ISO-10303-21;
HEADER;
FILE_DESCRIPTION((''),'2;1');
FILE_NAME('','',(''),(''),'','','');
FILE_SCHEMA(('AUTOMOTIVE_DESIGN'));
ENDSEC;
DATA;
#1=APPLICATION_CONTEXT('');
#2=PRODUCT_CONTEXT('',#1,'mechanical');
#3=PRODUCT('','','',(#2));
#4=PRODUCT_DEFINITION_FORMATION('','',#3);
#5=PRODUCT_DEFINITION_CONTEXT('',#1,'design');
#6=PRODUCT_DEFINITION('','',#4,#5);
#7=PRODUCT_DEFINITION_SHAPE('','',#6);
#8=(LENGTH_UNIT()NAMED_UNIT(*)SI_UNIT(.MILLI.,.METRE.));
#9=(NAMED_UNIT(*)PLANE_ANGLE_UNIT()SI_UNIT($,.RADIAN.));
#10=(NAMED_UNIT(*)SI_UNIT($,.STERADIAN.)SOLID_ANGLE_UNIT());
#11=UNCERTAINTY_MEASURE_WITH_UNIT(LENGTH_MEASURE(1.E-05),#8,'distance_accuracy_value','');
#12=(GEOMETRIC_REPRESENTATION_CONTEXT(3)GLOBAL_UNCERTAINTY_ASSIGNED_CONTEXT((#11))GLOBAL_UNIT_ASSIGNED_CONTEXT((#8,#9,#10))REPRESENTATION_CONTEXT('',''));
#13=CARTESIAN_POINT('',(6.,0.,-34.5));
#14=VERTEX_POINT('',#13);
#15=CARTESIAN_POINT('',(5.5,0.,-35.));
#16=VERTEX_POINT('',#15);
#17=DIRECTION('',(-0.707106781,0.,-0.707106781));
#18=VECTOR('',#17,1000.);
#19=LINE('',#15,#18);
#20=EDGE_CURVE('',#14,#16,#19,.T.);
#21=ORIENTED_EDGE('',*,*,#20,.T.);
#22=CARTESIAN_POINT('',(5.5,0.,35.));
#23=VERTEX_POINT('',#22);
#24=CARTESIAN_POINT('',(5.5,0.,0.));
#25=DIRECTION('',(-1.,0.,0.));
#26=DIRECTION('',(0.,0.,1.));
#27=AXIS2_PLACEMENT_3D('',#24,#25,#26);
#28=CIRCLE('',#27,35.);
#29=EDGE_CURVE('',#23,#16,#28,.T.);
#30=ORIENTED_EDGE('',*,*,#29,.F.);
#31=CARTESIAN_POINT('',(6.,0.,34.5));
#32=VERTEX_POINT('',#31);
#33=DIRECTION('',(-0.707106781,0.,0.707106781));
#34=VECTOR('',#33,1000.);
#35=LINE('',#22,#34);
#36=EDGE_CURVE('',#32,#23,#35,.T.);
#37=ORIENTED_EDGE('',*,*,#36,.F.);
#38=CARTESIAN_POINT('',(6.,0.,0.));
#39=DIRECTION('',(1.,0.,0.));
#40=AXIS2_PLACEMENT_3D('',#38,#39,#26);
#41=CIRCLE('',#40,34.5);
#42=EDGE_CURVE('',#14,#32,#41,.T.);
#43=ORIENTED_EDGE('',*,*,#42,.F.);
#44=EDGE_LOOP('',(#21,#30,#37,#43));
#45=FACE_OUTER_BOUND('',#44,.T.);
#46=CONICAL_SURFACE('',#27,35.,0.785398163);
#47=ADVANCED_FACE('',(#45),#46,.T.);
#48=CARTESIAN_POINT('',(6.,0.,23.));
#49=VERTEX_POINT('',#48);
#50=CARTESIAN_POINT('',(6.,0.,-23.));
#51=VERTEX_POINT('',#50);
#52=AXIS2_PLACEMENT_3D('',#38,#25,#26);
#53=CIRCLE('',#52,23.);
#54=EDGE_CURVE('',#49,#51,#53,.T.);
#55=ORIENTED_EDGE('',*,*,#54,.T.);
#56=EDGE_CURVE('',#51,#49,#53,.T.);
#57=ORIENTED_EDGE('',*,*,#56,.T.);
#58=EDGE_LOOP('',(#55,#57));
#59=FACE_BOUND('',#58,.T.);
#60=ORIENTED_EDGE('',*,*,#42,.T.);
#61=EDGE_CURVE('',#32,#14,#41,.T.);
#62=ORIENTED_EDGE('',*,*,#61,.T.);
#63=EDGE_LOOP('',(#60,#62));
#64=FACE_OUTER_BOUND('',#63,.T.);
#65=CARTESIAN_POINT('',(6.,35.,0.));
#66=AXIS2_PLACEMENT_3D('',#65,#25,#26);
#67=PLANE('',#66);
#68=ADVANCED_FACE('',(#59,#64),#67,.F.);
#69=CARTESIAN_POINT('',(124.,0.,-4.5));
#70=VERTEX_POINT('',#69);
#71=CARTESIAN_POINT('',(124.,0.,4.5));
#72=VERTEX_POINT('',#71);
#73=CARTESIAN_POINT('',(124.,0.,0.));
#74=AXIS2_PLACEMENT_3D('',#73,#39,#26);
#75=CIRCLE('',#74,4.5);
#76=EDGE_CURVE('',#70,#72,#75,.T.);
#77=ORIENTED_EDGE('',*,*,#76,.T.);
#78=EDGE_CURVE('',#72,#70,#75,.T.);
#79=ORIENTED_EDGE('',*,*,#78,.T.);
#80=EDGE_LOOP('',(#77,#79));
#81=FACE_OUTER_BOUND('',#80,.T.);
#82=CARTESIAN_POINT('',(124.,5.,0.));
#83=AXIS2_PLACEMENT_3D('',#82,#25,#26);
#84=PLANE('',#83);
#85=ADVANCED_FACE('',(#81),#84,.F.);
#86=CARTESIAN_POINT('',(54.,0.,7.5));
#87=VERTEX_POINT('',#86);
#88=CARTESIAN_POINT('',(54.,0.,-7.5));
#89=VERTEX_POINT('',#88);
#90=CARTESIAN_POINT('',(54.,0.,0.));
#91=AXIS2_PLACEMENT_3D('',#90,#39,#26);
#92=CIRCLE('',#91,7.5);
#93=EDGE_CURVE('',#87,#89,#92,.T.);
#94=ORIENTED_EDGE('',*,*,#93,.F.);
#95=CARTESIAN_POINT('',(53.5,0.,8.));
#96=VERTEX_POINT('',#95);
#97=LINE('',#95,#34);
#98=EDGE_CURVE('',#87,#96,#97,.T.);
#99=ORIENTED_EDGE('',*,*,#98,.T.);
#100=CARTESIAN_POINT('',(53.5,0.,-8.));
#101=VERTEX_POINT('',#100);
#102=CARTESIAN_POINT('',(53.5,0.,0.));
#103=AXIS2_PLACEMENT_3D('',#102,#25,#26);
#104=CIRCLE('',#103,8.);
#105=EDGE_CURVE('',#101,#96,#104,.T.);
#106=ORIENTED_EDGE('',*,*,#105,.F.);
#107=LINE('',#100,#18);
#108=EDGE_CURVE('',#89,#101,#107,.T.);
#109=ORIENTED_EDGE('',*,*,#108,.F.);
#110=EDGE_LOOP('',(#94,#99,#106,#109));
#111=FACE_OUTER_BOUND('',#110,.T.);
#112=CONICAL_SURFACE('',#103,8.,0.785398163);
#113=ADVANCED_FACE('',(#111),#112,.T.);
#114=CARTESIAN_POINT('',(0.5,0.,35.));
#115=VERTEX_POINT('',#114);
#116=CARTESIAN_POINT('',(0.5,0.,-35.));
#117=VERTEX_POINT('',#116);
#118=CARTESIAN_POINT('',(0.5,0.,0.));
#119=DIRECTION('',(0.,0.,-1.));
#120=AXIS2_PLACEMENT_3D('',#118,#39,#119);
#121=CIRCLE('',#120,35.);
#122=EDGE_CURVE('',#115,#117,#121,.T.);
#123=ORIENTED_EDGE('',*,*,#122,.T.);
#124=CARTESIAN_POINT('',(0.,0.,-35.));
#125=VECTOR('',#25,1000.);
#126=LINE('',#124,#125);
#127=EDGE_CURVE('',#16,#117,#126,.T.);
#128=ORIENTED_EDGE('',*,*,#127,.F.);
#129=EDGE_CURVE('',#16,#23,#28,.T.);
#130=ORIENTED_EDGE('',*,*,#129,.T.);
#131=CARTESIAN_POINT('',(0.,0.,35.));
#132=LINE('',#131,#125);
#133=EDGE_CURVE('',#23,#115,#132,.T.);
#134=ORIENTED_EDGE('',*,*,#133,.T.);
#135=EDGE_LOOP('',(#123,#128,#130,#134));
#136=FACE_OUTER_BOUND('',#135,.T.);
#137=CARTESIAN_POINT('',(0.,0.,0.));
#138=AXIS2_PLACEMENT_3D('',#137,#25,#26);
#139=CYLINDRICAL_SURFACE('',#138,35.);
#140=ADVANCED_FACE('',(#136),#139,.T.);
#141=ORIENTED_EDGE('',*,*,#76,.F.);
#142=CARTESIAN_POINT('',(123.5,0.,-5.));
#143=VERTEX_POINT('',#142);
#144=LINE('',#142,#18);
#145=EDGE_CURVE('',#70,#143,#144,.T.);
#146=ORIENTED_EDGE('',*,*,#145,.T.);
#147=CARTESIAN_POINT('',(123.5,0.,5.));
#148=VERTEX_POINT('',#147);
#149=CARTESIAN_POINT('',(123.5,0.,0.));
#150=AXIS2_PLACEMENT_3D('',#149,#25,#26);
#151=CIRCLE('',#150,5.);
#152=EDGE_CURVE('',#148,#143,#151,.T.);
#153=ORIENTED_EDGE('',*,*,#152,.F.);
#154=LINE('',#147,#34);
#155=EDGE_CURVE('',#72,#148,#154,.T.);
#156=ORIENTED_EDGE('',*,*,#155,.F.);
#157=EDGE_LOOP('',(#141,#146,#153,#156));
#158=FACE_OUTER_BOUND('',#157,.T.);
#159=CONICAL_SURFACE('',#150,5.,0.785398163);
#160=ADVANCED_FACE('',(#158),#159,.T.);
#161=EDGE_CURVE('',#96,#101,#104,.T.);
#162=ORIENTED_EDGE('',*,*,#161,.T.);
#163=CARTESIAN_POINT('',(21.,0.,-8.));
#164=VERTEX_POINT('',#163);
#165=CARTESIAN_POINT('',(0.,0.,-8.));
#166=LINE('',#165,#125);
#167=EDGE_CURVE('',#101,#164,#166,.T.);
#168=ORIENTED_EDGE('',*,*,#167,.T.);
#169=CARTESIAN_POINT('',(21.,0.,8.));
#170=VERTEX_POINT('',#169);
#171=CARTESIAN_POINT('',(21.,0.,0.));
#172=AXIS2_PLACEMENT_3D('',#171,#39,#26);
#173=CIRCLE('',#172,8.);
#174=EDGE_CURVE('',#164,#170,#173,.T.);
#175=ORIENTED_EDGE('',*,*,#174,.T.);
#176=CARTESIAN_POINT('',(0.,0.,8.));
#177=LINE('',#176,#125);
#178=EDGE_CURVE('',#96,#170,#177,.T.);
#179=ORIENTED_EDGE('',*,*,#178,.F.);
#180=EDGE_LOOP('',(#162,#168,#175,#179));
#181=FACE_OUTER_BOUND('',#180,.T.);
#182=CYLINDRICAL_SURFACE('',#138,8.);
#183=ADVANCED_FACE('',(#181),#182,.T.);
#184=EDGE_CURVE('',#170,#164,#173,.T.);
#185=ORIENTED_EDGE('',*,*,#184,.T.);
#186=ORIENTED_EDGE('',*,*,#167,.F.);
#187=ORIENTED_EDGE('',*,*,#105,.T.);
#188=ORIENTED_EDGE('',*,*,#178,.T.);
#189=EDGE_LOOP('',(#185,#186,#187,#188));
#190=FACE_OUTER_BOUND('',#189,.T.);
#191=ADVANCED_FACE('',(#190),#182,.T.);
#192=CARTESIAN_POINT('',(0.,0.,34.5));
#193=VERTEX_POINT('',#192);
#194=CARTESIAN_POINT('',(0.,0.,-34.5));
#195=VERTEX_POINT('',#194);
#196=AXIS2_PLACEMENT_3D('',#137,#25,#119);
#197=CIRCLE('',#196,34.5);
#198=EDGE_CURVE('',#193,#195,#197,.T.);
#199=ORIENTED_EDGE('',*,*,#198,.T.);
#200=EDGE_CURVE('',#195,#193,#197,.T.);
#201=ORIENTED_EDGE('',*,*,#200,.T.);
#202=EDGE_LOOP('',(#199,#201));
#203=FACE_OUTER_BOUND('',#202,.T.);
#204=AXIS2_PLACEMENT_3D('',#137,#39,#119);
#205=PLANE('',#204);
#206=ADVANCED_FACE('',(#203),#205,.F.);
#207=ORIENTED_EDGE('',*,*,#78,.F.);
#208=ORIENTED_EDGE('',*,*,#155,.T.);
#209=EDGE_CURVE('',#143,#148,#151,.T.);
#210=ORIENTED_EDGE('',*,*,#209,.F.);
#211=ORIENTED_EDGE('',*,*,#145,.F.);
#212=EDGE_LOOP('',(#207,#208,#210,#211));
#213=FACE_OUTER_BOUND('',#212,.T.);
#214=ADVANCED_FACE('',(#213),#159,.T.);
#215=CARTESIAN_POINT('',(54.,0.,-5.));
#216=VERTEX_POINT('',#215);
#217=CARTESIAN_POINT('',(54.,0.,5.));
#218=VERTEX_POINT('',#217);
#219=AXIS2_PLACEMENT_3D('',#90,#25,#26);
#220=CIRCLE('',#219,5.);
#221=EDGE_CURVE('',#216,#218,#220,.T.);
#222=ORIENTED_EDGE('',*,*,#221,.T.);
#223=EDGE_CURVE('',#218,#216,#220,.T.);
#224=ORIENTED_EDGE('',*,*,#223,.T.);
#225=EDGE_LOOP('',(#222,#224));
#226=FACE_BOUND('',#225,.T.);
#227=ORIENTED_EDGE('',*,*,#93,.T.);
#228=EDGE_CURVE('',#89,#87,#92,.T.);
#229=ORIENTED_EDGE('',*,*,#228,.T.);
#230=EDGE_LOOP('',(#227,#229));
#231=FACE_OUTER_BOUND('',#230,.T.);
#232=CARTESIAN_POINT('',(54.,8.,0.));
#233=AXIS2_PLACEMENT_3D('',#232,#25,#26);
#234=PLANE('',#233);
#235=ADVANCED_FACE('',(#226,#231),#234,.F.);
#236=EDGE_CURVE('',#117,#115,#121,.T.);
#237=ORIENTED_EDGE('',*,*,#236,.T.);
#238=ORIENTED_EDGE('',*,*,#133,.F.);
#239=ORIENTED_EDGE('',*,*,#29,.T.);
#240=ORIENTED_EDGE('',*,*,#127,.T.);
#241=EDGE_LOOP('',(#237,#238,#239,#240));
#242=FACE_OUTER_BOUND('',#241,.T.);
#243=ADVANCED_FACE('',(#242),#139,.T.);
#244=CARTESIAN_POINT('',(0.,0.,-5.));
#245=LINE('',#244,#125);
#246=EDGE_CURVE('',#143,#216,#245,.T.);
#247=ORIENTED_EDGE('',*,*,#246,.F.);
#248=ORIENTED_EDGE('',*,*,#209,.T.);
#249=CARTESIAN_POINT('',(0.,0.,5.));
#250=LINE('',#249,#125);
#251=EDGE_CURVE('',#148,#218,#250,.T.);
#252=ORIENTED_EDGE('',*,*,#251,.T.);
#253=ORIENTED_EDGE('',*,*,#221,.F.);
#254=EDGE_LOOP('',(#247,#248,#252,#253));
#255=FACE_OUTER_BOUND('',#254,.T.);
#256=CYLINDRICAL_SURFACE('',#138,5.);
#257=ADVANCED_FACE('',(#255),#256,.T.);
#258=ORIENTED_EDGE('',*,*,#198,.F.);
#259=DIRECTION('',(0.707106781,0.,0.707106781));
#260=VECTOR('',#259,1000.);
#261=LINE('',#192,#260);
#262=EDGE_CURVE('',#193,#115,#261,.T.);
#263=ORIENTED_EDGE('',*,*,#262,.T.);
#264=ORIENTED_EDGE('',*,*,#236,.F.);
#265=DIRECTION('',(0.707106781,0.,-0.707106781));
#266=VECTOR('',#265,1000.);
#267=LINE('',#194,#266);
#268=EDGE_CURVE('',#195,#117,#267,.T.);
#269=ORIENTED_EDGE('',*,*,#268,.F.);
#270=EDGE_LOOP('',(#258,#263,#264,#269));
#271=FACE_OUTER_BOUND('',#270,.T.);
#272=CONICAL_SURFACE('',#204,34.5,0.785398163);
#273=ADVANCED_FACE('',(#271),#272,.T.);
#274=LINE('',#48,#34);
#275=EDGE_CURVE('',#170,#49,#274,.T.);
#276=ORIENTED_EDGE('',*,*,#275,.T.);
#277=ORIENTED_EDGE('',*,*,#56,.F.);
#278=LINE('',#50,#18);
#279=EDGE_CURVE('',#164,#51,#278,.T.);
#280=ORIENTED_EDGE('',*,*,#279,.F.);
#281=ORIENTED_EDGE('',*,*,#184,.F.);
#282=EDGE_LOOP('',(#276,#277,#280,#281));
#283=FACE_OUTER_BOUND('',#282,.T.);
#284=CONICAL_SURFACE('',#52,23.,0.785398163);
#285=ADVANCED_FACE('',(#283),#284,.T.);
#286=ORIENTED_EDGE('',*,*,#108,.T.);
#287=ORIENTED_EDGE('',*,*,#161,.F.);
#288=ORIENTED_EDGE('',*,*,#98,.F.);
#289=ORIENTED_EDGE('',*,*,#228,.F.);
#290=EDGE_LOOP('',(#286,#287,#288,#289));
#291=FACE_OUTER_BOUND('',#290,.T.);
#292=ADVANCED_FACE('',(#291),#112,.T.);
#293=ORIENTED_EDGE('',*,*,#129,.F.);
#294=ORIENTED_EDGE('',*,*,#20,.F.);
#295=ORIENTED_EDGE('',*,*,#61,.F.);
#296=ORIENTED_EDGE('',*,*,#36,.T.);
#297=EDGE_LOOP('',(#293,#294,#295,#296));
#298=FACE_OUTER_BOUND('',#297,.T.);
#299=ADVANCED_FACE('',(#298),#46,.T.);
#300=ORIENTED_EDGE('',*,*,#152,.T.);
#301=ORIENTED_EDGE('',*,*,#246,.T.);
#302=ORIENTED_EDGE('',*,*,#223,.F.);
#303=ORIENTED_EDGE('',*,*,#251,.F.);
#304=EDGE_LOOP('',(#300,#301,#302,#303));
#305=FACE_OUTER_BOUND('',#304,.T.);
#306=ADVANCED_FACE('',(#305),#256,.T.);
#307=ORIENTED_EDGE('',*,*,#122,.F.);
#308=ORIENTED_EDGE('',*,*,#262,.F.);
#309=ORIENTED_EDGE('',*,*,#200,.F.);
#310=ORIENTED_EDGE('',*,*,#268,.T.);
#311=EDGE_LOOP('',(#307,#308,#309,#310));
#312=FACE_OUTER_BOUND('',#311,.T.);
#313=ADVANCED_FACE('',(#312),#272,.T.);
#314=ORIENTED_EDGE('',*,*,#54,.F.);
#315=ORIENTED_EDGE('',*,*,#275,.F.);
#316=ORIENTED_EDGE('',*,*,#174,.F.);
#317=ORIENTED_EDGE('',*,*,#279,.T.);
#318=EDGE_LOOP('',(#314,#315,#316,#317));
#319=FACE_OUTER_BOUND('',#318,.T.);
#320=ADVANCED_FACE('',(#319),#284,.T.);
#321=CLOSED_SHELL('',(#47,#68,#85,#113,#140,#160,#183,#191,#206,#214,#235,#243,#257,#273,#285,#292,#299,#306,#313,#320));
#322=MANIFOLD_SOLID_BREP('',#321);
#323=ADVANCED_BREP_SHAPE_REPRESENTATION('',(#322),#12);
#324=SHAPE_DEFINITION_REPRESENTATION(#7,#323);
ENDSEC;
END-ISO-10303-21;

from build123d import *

# Parameters (mm, degrees)
CHAMFER1_SIZE = 0.5
CHAMFER2_SIZE = 0.5
CHAMFER3_SIZE = 15


with BuildPart() as part:
    # Sketch1 → Revolve1 (revolve)
    with BuildSketch(Plane.XY, mode=Mode.PRIVATE) as revolve1_sk:
        Polygon((0, 0), (0, 35), (6, 35), (6, 8), (54, 8), (54, 5), (124, 5), (124, 0), align=None)
    revolve(revolve1_sk.sketch.rotate(Axis((0, 0, 0), (1, 0, 0)), 90), axis=Axis((0, 0, 0), (1, 0, 0)))

    # Chamfer1
    chamfer1_edges = [part.edges().sort_by_distance(p)[0] for p in [
        (54, 0, -8),
        (6, 0, -35),
        (0, 0, -35),
    ]]
    chamfer(chamfer1_edges, length=CHAMFER1_SIZE)

    # Chamfer2
    chamfer2_edges = [part.edges().sort_by_distance(p)[0] for p in [
        (124, 0, -5),
    ]]
    chamfer(chamfer2_edges, length=CHAMFER2_SIZE)

    # Chamfer3
    chamfer3_edges = [part.edges().sort_by_distance(p)[0] for p in [
        (6, 0, -8),
    ]]
    chamfer(chamfer3_edges, length=CHAMFER3_SIZE)


solid = part.part
